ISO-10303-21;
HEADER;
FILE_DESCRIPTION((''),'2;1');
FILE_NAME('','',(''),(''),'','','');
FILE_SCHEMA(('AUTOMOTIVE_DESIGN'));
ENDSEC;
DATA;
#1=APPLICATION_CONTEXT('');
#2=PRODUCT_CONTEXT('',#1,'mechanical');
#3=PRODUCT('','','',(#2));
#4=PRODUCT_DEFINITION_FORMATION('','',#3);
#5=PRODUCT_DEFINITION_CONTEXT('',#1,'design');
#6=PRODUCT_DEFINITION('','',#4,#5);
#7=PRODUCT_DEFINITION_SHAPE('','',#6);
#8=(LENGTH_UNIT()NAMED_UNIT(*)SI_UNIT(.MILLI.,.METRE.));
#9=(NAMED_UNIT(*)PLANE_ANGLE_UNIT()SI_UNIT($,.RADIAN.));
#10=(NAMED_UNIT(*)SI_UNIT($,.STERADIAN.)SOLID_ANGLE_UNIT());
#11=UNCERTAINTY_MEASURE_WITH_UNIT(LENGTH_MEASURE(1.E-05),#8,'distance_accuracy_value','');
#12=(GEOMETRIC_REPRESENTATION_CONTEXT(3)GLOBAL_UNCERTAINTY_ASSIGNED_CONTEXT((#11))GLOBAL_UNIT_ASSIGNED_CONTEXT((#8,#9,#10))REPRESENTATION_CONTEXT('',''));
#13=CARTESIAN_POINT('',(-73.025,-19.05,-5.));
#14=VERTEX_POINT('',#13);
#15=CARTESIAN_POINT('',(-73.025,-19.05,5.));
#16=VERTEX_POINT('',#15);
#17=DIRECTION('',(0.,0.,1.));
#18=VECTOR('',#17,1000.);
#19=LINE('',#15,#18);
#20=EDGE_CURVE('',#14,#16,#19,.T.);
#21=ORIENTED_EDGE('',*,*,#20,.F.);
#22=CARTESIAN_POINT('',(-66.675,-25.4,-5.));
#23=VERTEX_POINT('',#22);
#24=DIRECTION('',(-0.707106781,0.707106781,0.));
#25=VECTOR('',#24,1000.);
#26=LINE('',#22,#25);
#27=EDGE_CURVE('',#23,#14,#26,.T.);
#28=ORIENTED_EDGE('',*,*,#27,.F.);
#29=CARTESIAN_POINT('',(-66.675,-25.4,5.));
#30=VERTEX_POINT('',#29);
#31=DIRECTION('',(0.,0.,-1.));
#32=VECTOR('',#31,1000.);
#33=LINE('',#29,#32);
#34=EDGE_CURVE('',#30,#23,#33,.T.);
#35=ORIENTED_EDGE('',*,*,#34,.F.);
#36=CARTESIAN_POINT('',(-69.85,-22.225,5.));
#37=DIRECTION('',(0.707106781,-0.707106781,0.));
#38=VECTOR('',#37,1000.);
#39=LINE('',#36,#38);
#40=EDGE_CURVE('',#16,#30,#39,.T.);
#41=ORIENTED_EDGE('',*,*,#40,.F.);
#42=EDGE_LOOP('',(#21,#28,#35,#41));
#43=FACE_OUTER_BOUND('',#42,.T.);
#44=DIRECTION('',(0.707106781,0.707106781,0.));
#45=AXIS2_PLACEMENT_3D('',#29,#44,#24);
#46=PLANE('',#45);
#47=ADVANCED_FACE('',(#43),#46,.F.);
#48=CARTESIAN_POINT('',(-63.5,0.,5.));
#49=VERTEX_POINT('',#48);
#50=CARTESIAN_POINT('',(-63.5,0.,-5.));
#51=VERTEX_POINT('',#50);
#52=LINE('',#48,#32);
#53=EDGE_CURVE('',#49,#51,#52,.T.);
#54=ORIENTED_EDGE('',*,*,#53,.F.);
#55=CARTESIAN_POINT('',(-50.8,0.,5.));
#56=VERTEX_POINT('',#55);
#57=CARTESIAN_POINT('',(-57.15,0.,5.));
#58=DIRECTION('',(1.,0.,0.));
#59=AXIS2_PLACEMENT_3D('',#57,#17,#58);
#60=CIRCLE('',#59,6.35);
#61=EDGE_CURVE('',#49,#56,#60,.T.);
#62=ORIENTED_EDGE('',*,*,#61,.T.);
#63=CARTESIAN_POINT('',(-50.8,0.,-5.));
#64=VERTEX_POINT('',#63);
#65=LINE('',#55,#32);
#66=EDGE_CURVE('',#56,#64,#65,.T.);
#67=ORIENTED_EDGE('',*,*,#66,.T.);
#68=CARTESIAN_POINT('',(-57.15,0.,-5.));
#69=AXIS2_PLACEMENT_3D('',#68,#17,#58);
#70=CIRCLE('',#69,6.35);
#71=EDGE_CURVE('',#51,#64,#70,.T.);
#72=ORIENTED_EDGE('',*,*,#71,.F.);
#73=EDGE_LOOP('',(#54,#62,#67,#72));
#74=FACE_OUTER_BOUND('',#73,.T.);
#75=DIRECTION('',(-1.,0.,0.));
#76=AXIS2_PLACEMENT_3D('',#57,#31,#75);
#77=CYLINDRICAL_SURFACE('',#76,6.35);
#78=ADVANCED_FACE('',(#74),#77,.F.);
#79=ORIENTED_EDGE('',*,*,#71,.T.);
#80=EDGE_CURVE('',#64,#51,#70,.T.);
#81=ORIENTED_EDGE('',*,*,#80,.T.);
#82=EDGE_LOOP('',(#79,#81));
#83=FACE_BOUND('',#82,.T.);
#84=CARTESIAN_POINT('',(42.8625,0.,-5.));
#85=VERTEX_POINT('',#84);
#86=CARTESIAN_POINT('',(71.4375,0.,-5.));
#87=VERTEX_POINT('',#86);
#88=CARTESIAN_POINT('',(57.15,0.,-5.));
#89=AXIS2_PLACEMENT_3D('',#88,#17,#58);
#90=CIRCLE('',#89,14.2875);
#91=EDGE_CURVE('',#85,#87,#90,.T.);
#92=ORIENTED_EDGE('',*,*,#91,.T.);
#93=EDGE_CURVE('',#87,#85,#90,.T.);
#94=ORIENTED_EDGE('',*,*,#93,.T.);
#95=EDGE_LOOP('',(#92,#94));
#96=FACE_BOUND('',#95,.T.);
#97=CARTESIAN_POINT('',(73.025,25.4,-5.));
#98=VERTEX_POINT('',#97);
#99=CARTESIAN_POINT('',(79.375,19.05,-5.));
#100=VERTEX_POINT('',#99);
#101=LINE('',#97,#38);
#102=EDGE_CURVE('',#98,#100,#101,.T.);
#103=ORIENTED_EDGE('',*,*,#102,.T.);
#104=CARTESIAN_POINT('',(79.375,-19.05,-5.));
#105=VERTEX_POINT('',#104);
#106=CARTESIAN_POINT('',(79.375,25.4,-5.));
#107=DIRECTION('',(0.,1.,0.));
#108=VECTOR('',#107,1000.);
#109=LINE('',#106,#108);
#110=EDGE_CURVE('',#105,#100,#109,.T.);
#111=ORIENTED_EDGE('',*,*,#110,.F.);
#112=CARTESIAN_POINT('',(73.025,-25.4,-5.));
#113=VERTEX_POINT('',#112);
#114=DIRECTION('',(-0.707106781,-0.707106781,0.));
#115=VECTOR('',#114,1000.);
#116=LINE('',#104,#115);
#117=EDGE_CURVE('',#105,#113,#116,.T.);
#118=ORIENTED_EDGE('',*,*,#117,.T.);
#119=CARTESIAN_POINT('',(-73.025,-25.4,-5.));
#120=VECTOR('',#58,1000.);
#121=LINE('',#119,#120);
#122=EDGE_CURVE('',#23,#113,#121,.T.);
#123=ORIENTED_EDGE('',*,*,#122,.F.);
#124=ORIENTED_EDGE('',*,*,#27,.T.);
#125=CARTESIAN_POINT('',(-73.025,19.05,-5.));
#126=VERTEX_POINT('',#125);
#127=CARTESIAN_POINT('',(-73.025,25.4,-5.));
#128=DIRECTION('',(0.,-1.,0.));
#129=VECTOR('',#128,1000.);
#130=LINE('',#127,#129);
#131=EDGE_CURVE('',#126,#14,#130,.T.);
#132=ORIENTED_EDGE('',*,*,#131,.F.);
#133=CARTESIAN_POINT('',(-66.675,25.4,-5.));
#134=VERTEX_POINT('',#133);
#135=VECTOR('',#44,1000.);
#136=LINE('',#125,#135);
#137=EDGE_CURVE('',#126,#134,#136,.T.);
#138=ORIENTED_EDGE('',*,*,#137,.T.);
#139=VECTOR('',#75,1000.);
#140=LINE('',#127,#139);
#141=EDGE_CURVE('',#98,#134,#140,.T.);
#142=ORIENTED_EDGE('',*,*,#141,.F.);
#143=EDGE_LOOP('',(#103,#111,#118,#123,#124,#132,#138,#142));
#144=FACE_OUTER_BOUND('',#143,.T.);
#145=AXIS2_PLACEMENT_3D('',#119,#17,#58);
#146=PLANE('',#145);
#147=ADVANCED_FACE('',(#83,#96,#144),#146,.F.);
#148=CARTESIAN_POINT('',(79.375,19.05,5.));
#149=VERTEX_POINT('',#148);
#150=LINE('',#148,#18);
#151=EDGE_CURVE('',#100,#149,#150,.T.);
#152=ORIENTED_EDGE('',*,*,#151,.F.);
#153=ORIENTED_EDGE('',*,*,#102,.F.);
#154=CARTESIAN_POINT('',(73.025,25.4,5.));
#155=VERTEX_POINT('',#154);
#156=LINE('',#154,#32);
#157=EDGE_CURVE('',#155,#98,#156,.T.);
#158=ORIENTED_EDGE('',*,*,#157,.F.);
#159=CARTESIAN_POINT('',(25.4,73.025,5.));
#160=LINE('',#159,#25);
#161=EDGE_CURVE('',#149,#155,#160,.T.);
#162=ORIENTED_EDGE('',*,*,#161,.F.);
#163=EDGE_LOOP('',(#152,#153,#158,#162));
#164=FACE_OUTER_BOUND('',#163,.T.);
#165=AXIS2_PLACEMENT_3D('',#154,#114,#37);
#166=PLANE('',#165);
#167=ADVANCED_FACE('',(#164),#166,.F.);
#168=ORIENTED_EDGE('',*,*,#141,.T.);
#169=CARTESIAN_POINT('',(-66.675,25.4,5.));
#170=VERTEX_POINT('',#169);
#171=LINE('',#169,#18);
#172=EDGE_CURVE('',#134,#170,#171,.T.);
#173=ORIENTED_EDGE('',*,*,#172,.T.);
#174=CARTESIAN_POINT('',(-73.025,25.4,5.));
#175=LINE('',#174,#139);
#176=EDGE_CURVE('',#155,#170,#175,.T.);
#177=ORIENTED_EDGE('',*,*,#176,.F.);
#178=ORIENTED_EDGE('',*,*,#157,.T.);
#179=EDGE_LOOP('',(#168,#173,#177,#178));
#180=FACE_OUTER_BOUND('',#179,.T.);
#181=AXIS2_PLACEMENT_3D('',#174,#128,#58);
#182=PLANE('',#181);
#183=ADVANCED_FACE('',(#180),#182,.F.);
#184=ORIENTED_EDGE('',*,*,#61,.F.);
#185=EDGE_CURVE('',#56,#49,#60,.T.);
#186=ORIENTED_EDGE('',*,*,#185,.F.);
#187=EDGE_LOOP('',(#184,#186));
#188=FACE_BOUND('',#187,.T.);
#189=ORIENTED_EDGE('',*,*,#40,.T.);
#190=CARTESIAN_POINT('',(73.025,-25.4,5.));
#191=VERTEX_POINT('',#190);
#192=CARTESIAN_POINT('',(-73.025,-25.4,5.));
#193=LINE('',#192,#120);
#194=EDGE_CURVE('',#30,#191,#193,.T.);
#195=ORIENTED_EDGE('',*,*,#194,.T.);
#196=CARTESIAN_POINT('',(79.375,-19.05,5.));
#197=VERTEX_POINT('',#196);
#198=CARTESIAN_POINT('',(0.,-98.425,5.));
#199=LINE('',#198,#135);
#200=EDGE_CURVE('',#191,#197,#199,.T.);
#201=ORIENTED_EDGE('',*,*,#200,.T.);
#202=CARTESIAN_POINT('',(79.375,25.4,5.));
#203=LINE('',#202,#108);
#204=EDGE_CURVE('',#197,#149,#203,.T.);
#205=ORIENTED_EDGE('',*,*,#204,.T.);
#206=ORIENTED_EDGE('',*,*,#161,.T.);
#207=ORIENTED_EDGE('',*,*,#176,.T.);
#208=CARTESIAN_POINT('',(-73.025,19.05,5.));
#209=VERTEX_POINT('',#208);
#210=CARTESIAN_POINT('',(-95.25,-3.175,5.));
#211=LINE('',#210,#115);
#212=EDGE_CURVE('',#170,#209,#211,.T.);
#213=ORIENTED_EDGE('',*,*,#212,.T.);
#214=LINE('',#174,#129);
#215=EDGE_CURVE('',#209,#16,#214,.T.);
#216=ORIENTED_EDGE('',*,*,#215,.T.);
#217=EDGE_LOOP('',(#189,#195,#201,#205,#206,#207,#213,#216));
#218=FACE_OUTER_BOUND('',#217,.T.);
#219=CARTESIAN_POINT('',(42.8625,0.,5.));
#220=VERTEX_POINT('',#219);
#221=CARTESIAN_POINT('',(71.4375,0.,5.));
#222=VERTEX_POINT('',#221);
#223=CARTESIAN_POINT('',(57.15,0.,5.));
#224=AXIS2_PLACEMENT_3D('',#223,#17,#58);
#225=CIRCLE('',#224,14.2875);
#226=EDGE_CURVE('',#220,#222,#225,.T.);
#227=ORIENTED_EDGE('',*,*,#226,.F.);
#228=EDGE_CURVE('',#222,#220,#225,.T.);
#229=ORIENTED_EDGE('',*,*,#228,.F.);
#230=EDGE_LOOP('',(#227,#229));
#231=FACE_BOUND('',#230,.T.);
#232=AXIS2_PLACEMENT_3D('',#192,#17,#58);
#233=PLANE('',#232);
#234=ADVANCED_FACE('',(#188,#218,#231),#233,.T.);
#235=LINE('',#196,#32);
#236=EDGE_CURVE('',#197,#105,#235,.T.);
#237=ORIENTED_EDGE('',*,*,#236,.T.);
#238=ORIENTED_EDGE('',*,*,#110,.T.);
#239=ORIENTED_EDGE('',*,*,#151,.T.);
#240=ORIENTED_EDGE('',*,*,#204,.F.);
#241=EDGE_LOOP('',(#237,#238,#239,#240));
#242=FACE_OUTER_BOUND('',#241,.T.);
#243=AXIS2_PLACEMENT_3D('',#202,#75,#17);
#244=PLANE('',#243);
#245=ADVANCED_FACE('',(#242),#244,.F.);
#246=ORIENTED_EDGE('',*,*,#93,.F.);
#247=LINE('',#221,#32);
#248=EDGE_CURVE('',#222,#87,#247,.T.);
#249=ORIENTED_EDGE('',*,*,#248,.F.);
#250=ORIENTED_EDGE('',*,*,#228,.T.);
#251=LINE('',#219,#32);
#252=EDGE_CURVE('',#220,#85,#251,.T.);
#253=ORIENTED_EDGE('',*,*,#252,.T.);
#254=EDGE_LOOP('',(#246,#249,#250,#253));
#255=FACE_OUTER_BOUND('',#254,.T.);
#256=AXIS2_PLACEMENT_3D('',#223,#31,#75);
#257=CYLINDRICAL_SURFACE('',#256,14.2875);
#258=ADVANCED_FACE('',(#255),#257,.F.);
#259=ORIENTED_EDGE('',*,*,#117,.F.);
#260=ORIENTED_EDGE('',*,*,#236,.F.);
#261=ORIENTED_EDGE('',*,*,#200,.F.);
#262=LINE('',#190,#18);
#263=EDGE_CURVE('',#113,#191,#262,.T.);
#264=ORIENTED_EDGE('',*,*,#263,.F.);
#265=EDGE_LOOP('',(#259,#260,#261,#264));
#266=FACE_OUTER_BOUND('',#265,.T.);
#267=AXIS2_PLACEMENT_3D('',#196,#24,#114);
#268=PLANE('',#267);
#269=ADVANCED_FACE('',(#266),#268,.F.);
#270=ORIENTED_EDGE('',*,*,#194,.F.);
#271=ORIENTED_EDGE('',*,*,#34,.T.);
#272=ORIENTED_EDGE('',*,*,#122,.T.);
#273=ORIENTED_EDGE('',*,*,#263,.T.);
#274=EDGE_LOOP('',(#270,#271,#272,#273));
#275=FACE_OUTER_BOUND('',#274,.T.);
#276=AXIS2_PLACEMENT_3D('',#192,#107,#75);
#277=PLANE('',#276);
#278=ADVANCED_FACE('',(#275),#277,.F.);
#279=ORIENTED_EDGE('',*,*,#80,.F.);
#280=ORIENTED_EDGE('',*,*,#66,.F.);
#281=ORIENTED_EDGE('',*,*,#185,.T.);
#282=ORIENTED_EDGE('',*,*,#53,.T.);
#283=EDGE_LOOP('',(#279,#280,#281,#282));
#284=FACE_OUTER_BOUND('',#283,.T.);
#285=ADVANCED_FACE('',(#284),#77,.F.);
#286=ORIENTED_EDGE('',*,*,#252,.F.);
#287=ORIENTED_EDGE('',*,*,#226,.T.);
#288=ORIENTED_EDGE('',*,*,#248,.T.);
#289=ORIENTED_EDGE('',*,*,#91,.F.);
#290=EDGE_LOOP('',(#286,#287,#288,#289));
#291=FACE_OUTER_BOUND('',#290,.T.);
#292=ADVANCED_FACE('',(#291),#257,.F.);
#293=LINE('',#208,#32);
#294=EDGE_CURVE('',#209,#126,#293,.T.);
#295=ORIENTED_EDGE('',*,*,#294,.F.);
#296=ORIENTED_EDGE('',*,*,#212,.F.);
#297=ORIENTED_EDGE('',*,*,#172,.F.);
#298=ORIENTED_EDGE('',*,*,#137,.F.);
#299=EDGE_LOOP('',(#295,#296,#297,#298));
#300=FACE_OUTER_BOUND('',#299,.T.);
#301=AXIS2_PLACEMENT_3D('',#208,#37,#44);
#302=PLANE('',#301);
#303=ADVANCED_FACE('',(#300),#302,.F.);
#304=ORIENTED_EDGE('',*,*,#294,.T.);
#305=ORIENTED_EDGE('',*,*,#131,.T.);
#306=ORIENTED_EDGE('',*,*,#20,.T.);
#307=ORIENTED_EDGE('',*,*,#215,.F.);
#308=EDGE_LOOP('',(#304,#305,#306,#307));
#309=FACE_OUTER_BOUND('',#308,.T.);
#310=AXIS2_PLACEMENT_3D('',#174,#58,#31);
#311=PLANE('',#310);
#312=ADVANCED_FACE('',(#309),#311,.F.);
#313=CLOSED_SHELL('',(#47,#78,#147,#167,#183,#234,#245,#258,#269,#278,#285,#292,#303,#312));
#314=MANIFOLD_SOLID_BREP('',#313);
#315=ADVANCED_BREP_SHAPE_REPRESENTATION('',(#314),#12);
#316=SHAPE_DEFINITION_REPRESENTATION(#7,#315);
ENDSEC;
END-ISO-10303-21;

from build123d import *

# Parameters (mm, degrees)
SKETCH1_W      = 152.4
SKETCH1_H      = 50.8
SKETCH1_R      = 14.2875
SKETCH1_R_2    = 6.35
EXTRUDE1_DEPTH = 5
CHAMFER1_SIZE  = 6.35


with BuildPart() as part:
    # Sketch1 → Extrude1 (new, symmetric)
    with BuildSketch(Plane.XY):
        with Locations((3.175, 0)):
            Rectangle(SKETCH1_W, SKETCH1_H)
        with Locations((57.15, 0)):
            Circle(SKETCH1_R, mode=Mode.SUBTRACT)
        with Locations((-57.15, 0)):
            Circle(SKETCH1_R_2, mode=Mode.SUBTRACT)
    extrude(amount=EXTRUDE1_DEPTH, both=True)

    # Chamfer1
    chamfer1_edges = [part.edges().sort_by_distance(p)[0] for p in [
        (-73.025, 25.4, 0),
        (79.375, 25.4, 0),
        (79.375, -25.4, 0),
        (-73.025, -25.4, 0),
    ]]
    chamfer(chamfer1_edges, length=CHAMFER1_SIZE)


solid = part.part
